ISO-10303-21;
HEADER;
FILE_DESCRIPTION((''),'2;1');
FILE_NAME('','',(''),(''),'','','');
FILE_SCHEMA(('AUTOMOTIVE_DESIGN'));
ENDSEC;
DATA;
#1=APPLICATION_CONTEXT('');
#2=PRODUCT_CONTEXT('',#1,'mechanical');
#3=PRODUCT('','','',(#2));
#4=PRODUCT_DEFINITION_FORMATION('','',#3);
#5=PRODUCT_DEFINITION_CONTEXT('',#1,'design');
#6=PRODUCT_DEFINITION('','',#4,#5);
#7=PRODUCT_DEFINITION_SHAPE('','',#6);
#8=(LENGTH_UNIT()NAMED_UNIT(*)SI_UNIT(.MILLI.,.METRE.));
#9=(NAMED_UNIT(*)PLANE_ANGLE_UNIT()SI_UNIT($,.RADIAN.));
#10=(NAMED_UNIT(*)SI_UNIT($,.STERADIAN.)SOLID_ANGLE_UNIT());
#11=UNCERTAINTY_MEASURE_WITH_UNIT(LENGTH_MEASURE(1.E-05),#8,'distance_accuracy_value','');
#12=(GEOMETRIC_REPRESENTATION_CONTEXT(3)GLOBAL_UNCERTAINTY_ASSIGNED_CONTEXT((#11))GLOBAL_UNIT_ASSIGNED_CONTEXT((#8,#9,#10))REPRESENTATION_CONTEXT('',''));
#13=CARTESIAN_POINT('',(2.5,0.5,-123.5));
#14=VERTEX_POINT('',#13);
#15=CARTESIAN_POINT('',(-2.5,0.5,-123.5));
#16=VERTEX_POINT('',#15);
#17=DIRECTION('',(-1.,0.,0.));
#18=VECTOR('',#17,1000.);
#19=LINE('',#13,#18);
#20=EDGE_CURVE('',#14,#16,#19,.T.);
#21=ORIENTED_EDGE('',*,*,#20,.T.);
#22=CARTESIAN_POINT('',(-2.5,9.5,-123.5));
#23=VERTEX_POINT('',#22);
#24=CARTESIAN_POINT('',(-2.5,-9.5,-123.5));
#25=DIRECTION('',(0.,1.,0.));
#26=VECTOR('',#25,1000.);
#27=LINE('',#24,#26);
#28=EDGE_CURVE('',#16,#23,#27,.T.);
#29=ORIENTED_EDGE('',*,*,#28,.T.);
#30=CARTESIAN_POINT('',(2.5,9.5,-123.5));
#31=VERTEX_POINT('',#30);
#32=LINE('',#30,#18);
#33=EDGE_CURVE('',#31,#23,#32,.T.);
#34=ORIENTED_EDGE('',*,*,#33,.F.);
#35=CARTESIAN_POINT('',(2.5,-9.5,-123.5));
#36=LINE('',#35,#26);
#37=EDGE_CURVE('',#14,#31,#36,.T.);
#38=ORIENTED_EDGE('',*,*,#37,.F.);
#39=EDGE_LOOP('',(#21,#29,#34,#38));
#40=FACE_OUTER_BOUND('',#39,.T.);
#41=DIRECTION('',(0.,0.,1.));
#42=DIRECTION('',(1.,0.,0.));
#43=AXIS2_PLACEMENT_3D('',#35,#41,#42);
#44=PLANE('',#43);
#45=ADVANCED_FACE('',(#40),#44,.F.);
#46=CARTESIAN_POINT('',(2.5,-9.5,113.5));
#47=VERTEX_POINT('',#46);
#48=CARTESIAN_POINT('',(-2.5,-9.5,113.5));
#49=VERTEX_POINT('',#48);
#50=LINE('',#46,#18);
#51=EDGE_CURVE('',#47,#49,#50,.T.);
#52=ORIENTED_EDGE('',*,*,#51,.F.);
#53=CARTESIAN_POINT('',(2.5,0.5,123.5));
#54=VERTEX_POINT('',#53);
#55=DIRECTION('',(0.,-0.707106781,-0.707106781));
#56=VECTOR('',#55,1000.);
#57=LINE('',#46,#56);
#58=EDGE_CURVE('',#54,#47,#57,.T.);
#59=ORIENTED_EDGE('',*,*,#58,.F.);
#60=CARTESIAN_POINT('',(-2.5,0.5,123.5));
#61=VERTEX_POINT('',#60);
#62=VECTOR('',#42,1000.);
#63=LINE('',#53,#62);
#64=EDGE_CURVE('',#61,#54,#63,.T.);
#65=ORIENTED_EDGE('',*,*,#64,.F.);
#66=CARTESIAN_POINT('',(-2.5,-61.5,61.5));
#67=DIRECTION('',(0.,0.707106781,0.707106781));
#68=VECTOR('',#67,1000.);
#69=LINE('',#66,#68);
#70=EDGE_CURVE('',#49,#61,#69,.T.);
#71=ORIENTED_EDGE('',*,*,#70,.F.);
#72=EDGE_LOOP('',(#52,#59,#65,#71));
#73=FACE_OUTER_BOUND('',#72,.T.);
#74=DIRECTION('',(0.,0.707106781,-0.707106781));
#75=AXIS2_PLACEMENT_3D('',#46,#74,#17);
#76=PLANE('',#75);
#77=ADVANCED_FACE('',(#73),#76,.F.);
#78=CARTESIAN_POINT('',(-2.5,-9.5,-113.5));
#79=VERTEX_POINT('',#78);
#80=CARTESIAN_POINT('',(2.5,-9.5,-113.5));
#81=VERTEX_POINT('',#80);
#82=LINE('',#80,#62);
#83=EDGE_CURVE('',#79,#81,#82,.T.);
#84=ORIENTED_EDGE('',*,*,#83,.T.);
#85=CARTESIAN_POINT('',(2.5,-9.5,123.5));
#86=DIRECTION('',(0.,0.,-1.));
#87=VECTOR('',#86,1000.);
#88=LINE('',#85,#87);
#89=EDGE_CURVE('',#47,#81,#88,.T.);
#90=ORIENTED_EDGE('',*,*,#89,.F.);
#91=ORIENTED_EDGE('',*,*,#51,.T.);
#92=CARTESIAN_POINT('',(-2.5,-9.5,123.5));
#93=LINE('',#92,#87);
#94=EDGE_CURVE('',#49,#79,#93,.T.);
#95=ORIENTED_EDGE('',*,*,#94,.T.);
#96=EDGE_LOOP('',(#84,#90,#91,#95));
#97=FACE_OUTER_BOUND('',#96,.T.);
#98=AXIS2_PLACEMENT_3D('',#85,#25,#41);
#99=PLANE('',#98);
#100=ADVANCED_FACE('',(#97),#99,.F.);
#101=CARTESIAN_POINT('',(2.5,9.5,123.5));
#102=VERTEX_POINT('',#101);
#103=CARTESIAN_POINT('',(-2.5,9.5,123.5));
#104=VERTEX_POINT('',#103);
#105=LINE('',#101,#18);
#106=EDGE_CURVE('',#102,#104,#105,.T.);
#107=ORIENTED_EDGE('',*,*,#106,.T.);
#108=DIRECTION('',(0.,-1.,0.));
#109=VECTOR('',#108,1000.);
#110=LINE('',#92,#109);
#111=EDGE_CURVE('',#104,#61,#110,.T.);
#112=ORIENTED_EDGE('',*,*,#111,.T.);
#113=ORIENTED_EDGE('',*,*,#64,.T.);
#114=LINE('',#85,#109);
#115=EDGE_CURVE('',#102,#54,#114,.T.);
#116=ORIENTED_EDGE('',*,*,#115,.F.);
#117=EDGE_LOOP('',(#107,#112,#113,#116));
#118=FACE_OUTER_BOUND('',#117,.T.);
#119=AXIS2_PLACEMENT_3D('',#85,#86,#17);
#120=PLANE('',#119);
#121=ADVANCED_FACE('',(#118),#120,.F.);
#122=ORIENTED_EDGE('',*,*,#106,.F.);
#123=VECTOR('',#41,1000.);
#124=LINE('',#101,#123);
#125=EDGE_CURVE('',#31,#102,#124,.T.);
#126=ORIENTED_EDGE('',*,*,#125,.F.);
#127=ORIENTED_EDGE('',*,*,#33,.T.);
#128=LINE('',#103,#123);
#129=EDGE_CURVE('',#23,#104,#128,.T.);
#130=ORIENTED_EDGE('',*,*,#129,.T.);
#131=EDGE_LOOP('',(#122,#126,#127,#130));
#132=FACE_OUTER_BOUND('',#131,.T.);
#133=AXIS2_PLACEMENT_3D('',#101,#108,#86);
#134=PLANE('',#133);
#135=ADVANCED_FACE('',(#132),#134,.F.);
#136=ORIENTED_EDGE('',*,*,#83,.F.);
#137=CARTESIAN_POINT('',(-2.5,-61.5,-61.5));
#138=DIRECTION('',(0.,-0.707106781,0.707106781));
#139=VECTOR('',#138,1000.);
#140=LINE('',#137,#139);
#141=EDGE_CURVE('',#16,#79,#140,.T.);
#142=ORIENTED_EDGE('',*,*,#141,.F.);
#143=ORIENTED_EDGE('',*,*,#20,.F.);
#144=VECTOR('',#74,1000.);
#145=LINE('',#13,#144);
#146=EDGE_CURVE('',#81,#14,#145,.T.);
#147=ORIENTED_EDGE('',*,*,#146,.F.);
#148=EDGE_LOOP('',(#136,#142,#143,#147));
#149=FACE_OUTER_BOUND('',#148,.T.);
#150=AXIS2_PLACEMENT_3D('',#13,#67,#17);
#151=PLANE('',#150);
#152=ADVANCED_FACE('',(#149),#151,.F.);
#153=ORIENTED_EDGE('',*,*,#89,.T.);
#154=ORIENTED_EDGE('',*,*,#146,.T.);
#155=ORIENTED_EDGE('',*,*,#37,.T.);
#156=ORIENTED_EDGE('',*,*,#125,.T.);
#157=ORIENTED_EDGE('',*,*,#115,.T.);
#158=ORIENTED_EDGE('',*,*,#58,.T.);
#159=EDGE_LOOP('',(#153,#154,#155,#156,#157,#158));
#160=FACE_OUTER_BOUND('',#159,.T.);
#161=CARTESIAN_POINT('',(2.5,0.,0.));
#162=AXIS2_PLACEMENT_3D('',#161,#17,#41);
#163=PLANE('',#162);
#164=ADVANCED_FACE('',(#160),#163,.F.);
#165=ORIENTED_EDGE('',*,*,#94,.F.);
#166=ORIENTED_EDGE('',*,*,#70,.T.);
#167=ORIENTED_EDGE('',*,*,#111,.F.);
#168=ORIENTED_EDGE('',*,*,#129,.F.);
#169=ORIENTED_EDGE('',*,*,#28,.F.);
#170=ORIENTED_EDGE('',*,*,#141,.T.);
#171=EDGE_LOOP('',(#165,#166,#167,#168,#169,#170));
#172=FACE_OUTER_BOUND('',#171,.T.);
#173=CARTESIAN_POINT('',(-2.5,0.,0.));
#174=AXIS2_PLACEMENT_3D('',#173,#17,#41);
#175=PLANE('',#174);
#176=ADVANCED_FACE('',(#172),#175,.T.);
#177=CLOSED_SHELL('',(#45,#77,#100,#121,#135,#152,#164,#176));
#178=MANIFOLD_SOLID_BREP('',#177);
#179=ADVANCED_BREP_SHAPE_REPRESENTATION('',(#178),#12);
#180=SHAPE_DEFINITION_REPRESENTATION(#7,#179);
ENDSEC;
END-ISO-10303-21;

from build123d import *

# Parameters (mm, degrees)
SKETCH_1_W      = 247
SKETCH_1_H      = 19
EXTRUDE_1_DEPTH = 2.5
CHAMFER_1_SIZE  = 10


with BuildPart() as part:
    # 草图1 → 凸台-拉伸1 (new, symmetric)
    with BuildSketch(Plane(origin=(0, 0, 0), x_dir=(0, 0, -1), z_dir=(1, 0, 0))):
        Rectangle(SKETCH_1_W, SKETCH_1_H)
    extrude(amount=EXTRUDE_1_DEPTH, both=True)

    # 倒角1
    chamfer_1_edges = [part.edges().sort_by_distance(p)[0] for p in [
        (0, -9.5, -123.5),
        (0, -9.5, 123.5),
    ]]
    chamfer(chamfer_1_edges, length=CHAMFER_1_SIZE)


solid = part.part
